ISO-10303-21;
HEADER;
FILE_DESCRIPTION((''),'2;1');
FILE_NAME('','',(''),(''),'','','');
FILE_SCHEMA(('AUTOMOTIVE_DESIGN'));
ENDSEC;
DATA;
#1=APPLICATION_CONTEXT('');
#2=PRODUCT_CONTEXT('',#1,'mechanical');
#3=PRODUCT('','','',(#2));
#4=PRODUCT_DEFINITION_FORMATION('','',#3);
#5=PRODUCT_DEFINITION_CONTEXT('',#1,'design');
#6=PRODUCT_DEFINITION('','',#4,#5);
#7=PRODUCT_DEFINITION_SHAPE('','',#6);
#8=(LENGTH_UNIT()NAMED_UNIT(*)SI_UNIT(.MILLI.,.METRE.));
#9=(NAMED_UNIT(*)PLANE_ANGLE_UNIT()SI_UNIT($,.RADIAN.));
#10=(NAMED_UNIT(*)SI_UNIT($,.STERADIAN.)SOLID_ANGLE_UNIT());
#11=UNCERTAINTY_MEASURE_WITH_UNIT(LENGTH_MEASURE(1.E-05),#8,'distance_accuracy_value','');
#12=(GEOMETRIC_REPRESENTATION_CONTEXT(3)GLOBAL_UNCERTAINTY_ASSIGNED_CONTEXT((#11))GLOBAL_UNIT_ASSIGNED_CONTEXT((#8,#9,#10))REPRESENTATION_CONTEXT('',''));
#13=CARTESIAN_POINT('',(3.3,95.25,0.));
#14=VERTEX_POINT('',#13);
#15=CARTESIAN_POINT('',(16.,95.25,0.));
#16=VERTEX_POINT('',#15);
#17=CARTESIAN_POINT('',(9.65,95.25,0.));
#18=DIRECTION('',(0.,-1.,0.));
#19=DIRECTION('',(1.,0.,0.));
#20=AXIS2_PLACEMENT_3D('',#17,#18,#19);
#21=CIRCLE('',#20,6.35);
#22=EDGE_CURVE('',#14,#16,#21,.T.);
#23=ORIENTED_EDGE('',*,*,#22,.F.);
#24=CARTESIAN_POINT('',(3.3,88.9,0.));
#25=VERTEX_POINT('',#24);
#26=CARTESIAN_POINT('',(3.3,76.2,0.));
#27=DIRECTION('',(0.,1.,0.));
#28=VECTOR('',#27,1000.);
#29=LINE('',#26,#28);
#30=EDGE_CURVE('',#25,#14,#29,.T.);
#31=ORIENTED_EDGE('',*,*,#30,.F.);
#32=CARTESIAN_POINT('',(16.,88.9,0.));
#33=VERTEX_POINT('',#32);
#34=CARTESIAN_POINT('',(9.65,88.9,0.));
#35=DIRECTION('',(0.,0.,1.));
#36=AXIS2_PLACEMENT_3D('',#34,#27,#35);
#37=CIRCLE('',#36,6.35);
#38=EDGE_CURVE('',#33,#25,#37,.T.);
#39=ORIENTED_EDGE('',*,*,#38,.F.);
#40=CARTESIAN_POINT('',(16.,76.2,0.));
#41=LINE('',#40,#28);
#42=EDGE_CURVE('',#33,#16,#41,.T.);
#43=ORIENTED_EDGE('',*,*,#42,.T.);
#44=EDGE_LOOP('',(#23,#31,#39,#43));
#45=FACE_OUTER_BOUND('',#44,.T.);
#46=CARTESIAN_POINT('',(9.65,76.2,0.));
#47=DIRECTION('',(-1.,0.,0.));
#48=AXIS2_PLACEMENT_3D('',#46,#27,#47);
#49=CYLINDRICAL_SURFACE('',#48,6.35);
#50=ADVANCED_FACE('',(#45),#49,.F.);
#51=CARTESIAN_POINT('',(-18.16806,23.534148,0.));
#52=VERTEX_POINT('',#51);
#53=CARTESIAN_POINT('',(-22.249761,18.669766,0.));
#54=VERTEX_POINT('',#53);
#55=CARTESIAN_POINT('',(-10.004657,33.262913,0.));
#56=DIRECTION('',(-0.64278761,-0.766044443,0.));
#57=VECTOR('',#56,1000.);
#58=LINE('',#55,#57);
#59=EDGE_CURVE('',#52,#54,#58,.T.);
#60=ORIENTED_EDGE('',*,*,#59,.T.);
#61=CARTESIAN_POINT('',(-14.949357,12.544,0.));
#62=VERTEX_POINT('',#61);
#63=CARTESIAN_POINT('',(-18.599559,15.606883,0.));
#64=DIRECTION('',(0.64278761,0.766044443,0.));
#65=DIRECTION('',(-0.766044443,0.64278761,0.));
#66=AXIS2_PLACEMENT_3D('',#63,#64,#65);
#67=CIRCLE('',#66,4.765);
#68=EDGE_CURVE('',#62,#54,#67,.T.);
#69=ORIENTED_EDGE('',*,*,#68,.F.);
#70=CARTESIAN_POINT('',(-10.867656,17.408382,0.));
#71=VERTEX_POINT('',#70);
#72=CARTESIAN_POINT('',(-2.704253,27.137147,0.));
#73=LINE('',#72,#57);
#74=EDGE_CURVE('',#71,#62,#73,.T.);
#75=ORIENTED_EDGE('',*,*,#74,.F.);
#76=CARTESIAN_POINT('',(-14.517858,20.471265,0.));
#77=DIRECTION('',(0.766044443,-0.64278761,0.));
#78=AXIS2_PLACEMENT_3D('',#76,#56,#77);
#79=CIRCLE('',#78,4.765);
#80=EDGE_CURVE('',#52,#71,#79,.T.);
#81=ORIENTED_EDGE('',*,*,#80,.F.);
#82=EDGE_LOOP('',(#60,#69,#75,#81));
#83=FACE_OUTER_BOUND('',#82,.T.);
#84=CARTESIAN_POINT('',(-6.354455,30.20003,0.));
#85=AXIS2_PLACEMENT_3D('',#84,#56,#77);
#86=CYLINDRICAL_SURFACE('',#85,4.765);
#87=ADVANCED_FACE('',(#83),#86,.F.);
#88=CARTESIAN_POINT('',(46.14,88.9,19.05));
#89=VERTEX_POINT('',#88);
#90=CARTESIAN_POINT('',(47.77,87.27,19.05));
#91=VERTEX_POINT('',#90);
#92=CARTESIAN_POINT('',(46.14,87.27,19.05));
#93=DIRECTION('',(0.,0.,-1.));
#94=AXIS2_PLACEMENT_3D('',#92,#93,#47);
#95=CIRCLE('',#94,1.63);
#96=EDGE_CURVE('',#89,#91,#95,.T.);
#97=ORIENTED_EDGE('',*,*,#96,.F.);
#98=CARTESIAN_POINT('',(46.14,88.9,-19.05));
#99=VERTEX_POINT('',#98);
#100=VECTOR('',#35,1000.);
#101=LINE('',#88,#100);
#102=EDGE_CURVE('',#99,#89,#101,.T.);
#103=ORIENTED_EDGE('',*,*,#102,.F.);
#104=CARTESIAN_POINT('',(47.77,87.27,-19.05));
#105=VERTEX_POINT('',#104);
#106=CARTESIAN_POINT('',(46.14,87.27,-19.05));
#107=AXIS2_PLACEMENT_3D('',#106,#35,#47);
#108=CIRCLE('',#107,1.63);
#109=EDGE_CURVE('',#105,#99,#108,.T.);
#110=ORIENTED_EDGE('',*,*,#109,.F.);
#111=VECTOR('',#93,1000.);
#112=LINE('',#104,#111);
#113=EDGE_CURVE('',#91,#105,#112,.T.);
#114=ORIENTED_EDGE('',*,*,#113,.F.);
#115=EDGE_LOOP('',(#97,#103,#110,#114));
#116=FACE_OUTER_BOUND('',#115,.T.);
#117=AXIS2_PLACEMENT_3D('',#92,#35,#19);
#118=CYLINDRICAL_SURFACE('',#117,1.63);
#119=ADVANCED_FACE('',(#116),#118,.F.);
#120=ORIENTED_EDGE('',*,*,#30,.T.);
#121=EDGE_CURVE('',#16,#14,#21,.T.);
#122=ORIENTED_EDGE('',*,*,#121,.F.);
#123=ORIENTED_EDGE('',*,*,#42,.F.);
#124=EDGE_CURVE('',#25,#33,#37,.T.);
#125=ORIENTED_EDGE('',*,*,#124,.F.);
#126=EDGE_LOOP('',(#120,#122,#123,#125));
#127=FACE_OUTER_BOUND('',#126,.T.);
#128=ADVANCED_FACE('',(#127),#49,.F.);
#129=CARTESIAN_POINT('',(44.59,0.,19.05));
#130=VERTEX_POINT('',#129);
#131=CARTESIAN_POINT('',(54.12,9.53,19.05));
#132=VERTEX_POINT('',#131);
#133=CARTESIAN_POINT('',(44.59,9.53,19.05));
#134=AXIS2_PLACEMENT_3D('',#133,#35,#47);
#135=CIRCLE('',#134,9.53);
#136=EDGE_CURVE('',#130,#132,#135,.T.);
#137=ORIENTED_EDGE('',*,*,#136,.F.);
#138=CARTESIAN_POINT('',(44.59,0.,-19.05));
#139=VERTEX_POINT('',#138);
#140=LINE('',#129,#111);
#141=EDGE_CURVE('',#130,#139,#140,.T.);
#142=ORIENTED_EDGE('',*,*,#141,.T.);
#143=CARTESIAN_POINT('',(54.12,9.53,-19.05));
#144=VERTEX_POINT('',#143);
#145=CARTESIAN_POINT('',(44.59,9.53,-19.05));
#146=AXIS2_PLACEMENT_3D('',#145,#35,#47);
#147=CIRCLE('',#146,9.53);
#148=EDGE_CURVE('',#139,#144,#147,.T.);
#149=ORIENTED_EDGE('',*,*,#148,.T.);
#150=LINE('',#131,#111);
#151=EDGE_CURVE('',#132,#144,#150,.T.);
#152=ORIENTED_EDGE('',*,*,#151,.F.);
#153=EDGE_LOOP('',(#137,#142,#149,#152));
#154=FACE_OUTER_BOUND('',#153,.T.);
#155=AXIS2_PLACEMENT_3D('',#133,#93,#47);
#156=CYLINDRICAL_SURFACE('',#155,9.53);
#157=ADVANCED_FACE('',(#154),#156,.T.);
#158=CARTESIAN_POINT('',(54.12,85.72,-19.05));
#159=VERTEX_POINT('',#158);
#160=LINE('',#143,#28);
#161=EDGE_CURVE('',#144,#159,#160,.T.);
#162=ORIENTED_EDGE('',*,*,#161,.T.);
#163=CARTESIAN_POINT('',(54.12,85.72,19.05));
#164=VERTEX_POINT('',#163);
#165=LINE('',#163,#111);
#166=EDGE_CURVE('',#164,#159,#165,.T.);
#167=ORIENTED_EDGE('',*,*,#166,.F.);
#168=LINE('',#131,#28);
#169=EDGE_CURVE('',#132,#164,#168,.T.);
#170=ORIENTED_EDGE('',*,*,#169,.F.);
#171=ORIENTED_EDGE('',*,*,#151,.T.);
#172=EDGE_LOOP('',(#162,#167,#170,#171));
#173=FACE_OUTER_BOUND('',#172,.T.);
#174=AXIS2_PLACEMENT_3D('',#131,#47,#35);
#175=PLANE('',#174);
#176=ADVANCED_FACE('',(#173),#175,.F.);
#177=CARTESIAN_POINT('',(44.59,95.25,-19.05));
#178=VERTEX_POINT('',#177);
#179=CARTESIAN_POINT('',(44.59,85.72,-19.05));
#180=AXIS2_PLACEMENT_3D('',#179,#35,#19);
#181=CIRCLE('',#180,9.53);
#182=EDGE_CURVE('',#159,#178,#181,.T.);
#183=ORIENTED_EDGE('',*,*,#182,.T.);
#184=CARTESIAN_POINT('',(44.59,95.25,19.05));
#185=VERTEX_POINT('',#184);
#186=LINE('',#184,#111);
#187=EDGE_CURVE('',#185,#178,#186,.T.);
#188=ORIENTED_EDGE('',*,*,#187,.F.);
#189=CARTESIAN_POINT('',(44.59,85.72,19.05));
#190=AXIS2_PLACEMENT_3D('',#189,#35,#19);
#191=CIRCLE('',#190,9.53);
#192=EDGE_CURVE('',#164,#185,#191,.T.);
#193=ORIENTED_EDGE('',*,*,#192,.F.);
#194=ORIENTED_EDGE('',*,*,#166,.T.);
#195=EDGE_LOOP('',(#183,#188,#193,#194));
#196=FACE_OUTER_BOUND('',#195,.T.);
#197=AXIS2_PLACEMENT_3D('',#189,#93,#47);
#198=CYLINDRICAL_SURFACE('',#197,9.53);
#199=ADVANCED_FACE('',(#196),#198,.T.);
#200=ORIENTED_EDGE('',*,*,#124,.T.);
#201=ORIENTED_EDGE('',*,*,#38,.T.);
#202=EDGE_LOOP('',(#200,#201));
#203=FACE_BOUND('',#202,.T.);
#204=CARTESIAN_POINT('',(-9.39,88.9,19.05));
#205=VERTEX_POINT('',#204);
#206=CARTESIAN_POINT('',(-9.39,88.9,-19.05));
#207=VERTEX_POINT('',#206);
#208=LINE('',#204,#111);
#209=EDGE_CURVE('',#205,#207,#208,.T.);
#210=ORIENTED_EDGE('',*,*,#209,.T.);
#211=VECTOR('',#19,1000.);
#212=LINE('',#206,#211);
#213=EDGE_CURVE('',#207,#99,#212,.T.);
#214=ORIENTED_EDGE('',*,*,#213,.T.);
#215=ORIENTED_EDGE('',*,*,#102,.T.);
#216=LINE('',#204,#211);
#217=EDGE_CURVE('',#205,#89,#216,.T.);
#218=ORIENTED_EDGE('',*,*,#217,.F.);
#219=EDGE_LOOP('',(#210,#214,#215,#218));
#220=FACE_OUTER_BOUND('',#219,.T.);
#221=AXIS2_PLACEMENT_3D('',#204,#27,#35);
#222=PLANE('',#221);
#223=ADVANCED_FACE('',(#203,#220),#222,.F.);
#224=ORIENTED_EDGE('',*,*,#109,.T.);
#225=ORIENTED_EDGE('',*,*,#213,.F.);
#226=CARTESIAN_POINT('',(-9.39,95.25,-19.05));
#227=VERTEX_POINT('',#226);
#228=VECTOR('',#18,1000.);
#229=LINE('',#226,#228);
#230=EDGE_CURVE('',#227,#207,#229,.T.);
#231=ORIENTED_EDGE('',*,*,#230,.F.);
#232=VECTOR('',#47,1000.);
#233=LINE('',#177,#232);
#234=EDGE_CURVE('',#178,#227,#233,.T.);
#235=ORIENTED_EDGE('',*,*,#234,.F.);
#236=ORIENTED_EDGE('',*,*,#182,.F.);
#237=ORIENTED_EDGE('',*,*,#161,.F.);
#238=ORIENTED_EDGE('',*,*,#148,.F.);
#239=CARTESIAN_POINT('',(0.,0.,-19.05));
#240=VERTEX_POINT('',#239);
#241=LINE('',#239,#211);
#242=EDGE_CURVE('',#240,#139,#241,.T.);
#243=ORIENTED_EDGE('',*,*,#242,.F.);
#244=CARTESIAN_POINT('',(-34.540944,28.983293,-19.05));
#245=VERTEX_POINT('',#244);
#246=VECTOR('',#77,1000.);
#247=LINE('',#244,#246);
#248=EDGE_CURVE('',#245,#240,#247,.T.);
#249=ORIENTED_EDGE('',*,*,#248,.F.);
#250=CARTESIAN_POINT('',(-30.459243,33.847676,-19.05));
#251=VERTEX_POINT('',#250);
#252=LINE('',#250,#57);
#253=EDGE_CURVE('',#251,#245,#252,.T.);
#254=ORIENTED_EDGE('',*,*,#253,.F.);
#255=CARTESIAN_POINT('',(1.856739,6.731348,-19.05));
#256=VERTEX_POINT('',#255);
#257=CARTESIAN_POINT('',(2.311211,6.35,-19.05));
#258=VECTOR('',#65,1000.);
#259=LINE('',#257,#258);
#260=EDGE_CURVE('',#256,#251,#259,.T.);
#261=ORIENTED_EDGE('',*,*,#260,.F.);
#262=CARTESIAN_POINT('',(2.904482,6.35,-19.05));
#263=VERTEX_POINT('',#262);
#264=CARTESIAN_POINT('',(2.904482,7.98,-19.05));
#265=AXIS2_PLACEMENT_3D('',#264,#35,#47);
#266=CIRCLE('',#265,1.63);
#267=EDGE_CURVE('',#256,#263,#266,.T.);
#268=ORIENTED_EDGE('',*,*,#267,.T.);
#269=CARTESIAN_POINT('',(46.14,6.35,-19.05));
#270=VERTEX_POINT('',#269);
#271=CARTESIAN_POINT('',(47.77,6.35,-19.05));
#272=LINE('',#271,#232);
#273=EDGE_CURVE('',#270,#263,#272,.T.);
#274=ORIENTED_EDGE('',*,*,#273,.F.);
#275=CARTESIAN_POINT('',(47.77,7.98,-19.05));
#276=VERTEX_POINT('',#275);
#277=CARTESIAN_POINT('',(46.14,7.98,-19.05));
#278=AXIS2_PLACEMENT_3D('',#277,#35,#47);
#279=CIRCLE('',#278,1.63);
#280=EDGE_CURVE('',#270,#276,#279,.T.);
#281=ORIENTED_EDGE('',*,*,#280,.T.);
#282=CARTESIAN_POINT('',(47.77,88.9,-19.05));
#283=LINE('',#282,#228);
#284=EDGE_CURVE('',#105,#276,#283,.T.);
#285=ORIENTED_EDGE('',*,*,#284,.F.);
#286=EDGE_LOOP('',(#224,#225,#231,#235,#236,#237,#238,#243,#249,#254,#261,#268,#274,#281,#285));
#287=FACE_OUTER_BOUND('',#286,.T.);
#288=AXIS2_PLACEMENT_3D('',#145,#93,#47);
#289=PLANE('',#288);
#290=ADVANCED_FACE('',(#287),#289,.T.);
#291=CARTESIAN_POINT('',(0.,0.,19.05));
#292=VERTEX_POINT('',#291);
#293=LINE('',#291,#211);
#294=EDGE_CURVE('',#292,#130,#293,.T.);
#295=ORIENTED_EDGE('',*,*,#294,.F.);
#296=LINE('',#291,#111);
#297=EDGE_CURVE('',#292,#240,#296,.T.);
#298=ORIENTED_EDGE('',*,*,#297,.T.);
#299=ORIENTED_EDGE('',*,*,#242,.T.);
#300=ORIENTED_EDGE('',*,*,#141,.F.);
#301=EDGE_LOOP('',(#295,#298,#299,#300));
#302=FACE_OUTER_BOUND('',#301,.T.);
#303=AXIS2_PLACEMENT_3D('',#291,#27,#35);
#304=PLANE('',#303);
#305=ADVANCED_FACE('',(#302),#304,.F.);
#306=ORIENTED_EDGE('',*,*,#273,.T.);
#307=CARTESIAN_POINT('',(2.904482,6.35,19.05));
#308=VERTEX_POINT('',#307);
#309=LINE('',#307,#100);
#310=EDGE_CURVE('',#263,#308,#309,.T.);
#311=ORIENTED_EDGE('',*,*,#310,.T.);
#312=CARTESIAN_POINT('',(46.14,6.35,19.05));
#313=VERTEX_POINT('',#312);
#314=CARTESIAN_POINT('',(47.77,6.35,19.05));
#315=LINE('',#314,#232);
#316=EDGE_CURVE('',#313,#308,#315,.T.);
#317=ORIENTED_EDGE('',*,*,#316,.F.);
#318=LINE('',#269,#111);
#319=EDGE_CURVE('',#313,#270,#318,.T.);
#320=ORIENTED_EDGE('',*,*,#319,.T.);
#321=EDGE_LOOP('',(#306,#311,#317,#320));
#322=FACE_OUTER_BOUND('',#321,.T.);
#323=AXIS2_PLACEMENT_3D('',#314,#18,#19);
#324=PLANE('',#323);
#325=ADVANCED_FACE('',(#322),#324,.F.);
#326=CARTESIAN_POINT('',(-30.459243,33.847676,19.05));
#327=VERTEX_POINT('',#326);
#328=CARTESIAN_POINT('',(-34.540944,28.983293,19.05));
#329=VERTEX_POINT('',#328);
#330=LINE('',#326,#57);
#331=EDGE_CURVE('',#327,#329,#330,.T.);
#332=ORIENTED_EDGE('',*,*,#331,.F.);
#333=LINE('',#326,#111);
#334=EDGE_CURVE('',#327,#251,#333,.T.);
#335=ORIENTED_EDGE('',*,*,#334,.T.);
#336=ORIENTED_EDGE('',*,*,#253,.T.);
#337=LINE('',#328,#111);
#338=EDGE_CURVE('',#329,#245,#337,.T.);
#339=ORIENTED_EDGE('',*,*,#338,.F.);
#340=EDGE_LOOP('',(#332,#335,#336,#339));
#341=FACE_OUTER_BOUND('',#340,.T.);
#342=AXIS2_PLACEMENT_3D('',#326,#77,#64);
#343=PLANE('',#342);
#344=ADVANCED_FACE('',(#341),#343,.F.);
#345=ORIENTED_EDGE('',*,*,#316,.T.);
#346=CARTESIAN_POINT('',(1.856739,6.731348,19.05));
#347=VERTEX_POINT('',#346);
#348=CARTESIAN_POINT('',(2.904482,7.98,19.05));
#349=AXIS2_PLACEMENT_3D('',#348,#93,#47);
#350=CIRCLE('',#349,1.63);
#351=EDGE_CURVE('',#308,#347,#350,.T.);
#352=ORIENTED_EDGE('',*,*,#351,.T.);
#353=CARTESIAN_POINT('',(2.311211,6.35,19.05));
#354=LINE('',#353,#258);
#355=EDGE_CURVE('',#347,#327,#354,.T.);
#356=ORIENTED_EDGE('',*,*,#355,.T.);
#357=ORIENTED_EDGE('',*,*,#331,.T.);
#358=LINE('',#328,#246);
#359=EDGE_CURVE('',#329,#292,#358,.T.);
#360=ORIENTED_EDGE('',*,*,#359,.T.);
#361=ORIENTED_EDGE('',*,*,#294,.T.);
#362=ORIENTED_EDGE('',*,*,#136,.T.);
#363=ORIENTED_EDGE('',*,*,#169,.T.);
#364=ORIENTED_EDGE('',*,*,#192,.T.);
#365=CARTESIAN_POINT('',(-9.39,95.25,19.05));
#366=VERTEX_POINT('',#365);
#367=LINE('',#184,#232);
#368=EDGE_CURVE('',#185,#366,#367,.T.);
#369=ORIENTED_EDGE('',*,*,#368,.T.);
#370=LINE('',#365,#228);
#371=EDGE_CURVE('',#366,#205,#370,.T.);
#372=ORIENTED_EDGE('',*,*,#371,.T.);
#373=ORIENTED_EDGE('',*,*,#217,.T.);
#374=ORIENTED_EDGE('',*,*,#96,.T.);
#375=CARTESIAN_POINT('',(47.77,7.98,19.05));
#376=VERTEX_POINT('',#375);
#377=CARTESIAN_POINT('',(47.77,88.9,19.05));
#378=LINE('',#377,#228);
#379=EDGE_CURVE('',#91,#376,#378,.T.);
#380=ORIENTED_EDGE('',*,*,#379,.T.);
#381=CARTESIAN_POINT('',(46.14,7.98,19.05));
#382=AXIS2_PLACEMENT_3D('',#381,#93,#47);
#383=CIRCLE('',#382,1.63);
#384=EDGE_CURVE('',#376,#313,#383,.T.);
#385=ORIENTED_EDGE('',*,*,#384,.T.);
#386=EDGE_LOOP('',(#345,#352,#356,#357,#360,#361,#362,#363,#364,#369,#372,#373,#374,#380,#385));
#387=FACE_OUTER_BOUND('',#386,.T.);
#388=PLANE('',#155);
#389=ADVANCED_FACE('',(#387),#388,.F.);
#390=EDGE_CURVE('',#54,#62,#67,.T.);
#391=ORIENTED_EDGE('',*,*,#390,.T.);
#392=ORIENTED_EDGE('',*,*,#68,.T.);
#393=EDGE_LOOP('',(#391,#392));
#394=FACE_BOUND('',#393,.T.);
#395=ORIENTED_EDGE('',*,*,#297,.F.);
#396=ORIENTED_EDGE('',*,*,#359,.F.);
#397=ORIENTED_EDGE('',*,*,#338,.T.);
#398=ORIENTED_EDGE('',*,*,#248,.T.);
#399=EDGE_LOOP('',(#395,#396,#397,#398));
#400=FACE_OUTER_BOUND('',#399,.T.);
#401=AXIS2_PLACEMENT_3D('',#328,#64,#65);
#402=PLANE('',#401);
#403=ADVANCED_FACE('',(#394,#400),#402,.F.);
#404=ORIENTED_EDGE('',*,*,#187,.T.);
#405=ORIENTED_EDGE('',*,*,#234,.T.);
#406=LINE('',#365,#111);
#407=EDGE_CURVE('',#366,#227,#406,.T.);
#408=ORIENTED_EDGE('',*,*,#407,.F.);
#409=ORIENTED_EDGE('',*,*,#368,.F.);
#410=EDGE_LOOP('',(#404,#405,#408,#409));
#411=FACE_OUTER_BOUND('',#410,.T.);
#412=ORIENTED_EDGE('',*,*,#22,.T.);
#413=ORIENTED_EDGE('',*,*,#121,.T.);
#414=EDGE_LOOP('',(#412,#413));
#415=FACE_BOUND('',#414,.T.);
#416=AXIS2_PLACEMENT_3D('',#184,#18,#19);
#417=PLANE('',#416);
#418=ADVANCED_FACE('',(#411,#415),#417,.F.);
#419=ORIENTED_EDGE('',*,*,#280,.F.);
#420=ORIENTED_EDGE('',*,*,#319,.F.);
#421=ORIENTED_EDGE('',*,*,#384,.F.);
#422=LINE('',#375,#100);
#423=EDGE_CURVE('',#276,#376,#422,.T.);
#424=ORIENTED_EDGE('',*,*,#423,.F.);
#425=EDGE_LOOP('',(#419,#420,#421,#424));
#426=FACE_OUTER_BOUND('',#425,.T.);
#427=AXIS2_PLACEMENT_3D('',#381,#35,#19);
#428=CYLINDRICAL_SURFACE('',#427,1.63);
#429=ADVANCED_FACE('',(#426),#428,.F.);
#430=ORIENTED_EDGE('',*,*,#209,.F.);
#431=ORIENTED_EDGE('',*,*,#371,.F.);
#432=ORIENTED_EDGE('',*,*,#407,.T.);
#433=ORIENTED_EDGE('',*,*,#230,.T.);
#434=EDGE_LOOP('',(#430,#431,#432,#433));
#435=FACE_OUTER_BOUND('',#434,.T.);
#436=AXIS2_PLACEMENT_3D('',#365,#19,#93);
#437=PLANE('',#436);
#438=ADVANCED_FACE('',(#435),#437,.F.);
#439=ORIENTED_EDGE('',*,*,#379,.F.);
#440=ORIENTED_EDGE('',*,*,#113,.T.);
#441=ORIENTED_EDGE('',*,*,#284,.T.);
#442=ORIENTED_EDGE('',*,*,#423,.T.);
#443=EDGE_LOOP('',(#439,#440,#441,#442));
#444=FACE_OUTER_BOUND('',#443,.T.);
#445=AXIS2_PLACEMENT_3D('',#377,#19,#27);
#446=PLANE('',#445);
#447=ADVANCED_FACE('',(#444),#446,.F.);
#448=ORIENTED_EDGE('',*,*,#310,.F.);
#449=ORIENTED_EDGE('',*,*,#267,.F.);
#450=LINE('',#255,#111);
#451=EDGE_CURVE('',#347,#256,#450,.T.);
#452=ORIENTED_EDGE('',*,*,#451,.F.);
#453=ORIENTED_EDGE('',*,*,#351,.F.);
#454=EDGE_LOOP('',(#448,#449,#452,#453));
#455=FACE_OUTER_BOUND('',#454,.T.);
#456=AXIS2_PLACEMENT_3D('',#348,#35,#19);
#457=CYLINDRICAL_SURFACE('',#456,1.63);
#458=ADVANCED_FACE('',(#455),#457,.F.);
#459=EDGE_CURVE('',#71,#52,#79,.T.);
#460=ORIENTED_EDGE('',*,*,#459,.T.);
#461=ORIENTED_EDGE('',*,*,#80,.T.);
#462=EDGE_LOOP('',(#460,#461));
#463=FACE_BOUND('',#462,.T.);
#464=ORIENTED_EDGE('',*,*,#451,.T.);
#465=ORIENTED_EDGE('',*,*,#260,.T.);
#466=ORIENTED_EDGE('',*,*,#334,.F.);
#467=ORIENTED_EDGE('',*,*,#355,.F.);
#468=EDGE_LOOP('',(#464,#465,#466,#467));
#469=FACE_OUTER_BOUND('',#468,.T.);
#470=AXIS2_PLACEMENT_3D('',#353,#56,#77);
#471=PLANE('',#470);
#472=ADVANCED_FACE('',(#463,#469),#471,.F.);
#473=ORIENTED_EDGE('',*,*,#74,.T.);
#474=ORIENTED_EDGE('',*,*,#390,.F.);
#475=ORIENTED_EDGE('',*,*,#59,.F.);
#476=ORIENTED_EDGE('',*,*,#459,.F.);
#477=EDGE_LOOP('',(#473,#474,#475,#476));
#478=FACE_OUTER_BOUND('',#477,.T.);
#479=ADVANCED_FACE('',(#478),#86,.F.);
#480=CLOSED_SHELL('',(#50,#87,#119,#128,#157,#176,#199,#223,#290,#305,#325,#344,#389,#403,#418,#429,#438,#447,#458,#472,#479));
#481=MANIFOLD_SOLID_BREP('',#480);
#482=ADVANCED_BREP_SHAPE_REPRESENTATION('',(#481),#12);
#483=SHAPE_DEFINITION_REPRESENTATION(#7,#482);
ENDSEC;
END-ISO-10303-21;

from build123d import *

# Parameters (mm, degrees)
BRACKET_BODY_DEPTH     = 19.05
FLANGE_HOLE_A_SKETCH_R = 6.35
FLANGE_HOLE_A_DEPTH    = 19.05
FLANGE_HOLE_B_SKETCH_R = 4.765
FLANGE_HOLE_B_DEPTH    = 19.05
BEND_FILLET_R1_63_A_R  = 1.63
BEND_FILLET_R1_63_B_R  = 1.63


with BuildPart() as part:
    # Bracket Profile Sketch → Bracket Body (new, symmetric)
    with BuildSketch(Plane.XY):
        with BuildLine():
            Line((0, 0), (44.59, 0))
            ThreePointArc((44.59, 0), (51.328727625, 2.791272375), (54.12, 9.53))
            Line((54.12, 9.53), (54.12, 85.72))
            ThreePointArc((54.12, 85.72), (51.328727625, 92.458727625), (44.59, 95.25))
            Line((44.59, 95.25), (-9.39, 95.25))
            Line((-9.39, 95.25), (-9.39, 88.9))
            Line((-9.39, 88.9), (47.77, 88.9))
            Line((47.77, 88.9), (47.77, 6.35))
            Line((47.77, 6.35), (2.311210988, 6.35))
            Line((2.311210988, 6.35), (-30.459242619, 33.847675535))
            Line((-30.459242619, 33.847675535), (-34.54094394, 28.983293321))
            Line((-34.54094394, 28.983293321), (0, 0))
        make_face()
    extrude(amount=BRACKET_BODY_DEPTH, both=True)

    # Flange Hole A Sketch → Flange Hole A (cut, symmetric)
    with BuildSketch(Plane(origin=(0, 95.25, 0), x_dir=(1, 0, 0), z_dir=(0, 1, 0))):
        with Locations(Location((9.65, 0, 0), (0, 0, 180))):
            Circle(FLANGE_HOLE_A_SKETCH_R)
    extrude(amount=FLANGE_HOLE_A_DEPTH, both=True, mode=Mode.SUBTRACT)

    # Flange Hole B Sketch → Flange Hole B (cut, symmetric)
    with BuildSketch(Plane(origin=(0, 0, 0), x_dir=(0.7660444431189771, -0.6427876096865404, 0), z_dir=(-0.6427876096865404, -0.7660444431189771, 0))):
        with Locations((-24.28, 0)):
            Circle(FLANGE_HOLE_B_SKETCH_R)
    extrude(amount=FLANGE_HOLE_B_DEPTH, both=True, mode=Mode.SUBTRACT)

    # Bend Fillet R1.63 A
    bend_fillet_r1_63_a_edges = [part.edges().sort_by_distance(p)[0] for p in [
        (47.77, 6.35, 0),
        (47.77, 88.9, 0),
    ]]
    fillet(bend_fillet_r1_63_a_edges, radius=BEND_FILLET_R1_63_A_R)

    # Bend Fillet R1.63 B
    bend_fillet_r1_63_b_edges = [part.edges().sort_by_distance(p)[0] for p in [
        (2.311210988, 6.35, 0),
    ]]
    fillet(bend_fillet_r1_63_b_edges, radius=BEND_FILLET_R1_63_B_R)


solid = part.part
